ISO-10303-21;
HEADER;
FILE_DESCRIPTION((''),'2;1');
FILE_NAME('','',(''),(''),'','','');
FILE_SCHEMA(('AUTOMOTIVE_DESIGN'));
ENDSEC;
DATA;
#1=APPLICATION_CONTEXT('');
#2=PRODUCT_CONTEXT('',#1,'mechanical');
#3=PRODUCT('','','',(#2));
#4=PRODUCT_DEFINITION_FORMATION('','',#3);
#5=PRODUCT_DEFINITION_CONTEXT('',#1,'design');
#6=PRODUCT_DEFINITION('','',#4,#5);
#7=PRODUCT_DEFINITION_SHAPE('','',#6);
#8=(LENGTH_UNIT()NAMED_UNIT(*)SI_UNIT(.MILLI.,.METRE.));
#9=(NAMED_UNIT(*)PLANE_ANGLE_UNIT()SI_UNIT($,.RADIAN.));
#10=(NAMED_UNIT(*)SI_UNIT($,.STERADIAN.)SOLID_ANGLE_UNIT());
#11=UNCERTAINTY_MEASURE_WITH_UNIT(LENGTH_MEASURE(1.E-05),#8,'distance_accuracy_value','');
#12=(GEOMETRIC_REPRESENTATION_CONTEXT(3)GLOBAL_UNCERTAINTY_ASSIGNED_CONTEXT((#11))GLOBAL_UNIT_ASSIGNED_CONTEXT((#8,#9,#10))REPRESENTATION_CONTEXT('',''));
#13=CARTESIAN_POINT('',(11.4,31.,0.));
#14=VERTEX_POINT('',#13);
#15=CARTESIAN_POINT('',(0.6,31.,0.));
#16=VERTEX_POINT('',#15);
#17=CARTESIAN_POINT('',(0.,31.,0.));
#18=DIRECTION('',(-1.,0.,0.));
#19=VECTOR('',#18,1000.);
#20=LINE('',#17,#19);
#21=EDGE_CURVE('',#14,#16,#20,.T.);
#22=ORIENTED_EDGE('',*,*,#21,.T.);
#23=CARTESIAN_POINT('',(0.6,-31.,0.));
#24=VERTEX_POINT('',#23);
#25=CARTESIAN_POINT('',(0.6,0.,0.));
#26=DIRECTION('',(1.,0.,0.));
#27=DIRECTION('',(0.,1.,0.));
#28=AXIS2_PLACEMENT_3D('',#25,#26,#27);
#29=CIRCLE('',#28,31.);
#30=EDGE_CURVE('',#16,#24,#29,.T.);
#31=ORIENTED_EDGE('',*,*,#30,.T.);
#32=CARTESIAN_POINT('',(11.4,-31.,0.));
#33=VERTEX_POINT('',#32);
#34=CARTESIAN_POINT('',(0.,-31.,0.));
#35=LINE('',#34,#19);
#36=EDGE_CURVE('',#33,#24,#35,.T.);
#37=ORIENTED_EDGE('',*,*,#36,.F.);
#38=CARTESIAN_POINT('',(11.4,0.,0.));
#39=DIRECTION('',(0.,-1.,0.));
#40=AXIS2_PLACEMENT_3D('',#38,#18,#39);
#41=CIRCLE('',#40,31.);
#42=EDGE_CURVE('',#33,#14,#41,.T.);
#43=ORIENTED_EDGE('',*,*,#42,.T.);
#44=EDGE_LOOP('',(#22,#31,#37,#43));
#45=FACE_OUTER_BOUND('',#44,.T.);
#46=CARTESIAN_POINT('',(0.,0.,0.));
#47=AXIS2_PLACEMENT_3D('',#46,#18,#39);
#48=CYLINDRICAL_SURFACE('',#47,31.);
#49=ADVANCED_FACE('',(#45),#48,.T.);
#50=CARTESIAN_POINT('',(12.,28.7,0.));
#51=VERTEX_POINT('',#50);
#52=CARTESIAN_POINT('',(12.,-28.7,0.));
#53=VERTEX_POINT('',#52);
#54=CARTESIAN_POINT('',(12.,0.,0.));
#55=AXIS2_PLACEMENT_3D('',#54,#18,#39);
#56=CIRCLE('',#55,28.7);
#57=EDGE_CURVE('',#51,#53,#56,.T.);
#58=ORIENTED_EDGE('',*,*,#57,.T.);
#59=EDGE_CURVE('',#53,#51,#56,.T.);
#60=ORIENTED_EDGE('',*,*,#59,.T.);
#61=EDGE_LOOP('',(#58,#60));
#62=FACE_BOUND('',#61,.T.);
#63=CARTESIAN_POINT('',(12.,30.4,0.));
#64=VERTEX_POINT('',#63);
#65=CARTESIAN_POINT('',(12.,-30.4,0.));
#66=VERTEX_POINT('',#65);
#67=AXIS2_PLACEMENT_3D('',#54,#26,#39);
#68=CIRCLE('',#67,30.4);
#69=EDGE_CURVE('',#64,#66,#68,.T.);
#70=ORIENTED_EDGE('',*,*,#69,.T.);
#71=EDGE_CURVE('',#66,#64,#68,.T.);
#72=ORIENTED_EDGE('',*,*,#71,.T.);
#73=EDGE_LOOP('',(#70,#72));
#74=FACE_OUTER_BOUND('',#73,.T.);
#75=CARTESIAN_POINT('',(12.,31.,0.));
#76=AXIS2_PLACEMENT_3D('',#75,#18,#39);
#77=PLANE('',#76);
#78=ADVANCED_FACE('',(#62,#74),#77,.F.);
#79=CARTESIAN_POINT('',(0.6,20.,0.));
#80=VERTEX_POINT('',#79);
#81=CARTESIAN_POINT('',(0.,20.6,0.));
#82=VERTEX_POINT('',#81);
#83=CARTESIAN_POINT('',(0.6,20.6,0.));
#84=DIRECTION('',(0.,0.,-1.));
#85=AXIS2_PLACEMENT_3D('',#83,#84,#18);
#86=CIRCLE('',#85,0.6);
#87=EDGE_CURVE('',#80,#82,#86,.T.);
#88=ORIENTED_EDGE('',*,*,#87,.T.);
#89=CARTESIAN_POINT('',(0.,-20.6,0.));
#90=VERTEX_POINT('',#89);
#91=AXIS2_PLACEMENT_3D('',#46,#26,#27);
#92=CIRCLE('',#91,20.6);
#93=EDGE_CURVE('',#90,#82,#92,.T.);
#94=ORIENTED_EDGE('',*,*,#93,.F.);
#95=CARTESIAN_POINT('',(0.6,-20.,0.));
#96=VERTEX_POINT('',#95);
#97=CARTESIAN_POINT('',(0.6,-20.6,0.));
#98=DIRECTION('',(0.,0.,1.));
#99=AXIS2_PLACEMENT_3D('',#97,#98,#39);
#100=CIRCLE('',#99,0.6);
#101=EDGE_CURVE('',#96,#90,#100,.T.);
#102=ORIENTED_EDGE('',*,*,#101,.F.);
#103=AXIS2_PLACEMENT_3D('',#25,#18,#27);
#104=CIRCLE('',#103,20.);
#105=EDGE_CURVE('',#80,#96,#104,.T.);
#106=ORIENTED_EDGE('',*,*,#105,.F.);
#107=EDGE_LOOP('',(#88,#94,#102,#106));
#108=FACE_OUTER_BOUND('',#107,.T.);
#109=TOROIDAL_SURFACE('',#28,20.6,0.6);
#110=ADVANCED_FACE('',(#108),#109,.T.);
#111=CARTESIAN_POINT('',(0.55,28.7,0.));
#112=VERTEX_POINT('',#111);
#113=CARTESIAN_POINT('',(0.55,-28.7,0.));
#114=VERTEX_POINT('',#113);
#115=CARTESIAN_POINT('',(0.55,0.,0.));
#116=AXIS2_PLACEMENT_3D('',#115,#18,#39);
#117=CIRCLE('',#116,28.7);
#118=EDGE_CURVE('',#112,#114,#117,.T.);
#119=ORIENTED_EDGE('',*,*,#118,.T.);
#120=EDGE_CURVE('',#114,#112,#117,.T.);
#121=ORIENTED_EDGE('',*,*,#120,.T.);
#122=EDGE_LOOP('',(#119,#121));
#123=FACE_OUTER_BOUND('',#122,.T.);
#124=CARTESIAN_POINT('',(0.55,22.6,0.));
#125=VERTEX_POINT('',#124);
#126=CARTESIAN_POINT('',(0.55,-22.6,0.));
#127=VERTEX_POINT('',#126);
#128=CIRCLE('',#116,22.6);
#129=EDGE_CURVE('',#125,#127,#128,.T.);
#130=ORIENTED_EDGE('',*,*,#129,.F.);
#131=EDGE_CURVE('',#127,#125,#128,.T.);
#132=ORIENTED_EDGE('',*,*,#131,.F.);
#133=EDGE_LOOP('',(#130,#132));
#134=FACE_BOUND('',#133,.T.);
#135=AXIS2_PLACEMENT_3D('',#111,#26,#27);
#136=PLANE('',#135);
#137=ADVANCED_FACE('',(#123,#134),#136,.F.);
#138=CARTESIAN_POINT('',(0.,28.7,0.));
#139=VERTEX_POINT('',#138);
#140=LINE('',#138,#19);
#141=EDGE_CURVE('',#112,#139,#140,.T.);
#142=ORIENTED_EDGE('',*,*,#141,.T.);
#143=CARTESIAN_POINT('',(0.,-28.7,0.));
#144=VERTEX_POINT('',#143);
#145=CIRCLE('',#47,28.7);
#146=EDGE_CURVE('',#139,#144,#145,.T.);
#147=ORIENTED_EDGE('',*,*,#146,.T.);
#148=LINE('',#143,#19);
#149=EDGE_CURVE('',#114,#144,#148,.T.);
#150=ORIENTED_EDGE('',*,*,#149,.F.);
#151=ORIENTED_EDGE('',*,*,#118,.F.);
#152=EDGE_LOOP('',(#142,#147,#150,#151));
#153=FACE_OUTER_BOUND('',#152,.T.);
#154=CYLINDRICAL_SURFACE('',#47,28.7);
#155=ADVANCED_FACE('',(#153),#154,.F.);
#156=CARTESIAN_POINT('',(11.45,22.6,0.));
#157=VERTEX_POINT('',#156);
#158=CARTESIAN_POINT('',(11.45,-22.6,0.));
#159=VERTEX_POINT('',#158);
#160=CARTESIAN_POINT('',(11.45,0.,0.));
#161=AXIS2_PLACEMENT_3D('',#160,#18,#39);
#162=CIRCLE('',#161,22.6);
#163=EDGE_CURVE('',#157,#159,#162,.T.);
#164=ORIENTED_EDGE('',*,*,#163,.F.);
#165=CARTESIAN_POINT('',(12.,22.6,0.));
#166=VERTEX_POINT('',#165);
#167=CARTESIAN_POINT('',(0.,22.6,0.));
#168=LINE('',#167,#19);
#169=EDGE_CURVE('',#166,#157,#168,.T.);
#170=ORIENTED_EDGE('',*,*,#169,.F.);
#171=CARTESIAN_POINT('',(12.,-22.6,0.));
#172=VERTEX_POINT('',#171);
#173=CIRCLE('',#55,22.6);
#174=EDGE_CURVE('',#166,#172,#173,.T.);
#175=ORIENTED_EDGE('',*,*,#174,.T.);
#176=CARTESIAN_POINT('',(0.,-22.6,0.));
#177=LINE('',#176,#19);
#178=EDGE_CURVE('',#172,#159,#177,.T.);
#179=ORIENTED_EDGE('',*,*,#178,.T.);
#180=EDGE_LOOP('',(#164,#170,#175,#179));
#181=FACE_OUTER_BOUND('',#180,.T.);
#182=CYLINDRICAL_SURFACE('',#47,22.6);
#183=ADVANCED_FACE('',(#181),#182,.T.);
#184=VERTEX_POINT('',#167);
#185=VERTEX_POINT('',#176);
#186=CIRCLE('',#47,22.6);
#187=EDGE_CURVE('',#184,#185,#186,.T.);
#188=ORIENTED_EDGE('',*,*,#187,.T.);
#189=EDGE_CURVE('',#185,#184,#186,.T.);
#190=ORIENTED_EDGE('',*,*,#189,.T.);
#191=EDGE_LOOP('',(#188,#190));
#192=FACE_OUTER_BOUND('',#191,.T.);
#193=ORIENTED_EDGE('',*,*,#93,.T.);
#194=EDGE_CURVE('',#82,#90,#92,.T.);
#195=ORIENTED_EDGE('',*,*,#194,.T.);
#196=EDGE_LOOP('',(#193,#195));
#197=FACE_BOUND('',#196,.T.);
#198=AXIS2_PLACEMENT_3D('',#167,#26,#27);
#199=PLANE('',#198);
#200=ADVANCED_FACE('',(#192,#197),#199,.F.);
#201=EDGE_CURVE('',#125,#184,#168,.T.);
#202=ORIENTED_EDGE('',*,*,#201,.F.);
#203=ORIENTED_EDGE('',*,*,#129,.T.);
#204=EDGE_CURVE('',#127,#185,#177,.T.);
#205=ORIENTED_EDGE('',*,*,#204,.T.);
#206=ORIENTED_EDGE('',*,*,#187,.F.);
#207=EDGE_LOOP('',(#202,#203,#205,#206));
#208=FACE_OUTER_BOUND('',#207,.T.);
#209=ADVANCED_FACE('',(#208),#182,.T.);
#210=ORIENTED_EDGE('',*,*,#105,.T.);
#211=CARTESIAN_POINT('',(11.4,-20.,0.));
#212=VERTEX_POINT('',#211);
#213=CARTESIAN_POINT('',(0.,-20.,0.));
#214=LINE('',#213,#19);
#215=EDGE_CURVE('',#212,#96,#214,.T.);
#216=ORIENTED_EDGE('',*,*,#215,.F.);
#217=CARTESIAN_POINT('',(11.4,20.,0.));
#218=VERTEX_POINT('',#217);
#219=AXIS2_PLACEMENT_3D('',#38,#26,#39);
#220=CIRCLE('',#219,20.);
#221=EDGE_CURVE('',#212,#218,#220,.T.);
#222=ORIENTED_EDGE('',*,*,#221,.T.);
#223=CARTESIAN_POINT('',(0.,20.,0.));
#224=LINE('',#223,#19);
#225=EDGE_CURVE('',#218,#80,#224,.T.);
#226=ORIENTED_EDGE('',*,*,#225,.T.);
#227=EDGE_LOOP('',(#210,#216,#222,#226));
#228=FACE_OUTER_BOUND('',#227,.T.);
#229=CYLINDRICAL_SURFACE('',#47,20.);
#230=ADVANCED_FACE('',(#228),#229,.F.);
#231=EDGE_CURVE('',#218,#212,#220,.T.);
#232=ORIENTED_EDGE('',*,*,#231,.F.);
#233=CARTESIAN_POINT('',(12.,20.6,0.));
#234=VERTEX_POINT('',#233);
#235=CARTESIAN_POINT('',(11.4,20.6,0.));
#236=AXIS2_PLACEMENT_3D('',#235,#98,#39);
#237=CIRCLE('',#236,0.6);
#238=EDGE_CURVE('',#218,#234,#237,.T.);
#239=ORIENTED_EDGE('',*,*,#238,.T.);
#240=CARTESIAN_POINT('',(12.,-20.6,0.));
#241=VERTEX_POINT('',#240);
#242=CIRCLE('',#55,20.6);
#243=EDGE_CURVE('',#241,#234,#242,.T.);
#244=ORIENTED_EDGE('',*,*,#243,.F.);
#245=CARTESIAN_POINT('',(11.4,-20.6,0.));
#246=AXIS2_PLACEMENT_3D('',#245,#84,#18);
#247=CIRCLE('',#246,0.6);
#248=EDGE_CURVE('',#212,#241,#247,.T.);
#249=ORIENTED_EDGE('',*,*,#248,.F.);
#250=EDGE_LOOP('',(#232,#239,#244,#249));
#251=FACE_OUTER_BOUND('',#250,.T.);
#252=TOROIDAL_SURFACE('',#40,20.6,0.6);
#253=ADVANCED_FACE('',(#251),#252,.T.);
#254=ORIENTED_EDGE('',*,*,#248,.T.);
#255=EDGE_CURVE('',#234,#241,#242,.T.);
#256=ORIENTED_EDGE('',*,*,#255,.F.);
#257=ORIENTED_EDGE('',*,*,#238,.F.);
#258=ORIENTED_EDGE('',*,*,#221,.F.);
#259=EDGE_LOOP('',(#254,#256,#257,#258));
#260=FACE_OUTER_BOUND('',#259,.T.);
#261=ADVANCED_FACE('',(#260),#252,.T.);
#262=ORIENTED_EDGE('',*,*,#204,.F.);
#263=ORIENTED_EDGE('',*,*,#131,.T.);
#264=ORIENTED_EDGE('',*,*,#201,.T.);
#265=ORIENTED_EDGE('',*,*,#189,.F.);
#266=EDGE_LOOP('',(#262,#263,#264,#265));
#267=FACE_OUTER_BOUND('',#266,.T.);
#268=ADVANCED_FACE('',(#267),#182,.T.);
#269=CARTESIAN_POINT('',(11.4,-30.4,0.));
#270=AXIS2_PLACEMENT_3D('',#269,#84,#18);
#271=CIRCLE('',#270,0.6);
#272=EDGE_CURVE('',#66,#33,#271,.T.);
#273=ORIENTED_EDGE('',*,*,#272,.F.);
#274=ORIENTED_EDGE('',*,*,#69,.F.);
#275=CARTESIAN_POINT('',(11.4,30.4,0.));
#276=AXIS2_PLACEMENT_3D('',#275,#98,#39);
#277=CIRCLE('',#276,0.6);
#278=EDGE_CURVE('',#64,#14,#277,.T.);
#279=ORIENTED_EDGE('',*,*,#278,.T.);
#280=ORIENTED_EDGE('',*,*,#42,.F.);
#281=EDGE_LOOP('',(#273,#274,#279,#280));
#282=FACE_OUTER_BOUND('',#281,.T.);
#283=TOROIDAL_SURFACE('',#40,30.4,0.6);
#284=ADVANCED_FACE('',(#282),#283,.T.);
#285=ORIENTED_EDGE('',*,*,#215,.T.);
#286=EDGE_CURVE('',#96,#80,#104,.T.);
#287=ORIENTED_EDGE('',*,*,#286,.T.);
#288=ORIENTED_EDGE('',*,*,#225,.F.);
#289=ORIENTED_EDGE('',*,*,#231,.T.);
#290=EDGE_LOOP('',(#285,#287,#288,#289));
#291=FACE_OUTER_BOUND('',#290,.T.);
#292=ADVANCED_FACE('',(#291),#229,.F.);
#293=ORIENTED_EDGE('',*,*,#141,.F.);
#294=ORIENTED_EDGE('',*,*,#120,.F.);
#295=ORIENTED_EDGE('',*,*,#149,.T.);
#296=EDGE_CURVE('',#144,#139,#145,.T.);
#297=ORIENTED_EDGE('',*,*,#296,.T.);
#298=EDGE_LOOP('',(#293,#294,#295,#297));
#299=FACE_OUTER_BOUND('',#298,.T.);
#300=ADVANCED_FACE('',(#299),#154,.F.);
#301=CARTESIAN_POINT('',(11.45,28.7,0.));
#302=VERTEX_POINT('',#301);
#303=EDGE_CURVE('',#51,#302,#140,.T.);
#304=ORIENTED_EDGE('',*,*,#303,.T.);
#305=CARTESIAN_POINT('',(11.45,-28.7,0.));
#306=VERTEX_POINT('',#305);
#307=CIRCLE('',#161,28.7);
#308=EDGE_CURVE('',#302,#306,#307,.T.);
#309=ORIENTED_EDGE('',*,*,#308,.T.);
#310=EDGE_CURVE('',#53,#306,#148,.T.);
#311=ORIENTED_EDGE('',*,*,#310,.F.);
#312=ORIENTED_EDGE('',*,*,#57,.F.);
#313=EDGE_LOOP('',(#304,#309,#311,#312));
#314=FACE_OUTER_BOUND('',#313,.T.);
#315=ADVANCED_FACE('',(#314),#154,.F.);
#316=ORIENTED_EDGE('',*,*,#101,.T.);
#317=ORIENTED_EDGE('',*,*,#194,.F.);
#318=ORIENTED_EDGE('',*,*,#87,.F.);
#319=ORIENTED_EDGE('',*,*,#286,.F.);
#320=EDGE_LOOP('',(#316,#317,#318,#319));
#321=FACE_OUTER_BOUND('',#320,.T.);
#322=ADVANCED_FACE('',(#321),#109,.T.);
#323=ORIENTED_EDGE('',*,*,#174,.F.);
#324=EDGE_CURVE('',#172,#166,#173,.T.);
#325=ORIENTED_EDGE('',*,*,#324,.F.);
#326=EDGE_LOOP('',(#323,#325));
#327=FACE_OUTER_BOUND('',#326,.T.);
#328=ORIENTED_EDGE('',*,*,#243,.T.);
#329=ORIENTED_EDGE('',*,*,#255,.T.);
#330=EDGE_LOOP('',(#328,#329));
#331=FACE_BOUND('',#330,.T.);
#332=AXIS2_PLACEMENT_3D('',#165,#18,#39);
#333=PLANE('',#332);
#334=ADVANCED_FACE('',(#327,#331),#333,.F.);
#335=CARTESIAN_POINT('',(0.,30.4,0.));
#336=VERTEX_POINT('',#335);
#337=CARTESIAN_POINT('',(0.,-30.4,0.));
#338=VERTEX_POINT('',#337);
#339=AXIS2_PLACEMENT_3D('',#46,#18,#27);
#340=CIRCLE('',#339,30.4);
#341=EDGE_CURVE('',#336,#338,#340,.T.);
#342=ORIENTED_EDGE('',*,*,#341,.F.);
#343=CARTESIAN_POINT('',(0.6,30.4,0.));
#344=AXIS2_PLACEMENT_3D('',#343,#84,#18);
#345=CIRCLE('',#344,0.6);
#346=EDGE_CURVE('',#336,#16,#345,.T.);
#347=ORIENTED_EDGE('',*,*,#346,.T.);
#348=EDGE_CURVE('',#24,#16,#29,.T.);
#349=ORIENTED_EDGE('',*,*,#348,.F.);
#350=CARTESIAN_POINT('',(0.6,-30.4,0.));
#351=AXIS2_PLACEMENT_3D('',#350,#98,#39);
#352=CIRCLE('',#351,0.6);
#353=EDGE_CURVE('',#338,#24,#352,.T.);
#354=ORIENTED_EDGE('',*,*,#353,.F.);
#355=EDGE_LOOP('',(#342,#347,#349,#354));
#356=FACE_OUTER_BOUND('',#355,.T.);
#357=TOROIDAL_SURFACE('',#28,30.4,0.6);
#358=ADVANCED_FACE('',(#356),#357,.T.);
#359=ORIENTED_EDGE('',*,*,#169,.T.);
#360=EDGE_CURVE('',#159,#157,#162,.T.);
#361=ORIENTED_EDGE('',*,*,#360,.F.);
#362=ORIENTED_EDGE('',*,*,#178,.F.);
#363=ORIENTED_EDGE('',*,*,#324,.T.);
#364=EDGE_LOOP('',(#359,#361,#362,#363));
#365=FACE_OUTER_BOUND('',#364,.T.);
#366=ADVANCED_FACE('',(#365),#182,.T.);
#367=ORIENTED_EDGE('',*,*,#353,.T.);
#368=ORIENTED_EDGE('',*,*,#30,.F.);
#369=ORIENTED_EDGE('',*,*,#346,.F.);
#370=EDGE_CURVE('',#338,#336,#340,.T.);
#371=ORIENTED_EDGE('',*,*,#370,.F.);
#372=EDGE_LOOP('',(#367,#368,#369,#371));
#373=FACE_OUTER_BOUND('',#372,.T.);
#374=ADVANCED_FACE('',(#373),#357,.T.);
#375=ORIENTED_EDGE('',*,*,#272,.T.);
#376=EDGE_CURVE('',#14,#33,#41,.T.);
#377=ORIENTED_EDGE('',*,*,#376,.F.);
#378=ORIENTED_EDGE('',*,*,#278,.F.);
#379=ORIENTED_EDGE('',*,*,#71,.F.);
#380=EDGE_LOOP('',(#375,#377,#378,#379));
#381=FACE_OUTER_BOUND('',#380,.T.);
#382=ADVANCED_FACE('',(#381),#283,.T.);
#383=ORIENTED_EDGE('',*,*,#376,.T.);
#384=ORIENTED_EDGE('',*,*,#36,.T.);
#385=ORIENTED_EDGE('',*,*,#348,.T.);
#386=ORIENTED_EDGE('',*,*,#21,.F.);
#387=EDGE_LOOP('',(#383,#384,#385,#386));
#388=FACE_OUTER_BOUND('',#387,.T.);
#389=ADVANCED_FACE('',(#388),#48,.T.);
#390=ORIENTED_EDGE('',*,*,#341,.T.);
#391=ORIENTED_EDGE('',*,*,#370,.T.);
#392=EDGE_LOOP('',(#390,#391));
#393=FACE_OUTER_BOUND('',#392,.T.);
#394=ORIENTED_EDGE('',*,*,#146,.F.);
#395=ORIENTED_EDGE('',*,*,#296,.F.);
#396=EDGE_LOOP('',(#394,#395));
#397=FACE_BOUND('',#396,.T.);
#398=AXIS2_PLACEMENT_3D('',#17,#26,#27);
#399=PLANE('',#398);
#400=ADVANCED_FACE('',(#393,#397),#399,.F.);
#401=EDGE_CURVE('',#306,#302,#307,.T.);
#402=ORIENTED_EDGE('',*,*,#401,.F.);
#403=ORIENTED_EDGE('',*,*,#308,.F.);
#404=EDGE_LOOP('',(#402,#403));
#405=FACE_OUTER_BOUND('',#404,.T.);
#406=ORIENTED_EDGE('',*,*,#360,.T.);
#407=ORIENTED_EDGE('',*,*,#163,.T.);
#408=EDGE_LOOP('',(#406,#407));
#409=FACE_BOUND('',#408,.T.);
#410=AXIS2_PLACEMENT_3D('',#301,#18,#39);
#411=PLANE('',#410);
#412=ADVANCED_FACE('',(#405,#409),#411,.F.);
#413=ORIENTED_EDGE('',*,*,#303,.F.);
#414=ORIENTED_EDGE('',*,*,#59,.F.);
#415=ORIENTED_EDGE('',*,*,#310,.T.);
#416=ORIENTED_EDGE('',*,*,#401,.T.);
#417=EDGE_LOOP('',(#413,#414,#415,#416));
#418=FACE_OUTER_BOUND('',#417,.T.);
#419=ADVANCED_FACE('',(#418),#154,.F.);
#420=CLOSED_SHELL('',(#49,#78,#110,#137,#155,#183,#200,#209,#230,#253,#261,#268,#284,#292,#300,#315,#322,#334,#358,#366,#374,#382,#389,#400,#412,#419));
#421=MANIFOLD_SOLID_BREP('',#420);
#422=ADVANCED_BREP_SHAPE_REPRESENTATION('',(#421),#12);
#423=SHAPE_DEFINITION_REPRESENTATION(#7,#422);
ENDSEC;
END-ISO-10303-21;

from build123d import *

# Parameters (mm, degrees)
FILLET1_R = 0.6
FILLET2_R = 0.6


with BuildPart() as part:
    # Sketch1 → Revolve1 (revolve)
    with BuildSketch(Plane.XY, mode=Mode.PRIVATE) as revolve1_sk:
        Polygon((0, 20), (12, 20), (12, 22.6), (11.45, 22.6), (11.45, 28.7), (12, 28.7), (12, 31), (0, 31), (0, 28.7), (0.55, 28.7), (0.55, 22.6), (0, 22.6), align=None)
    revolve(revolve1_sk.sketch.rotate(Axis((0, 0, 0), (1, 0, 0)), 180), axis=Axis((0, 0, 0), (1, 0, 0)))

    # Fillet1
    fillet1_edges = [part.edges().sort_by_distance(p)[0] for p in [
        (0, 31, 0),
        (12, 31, 0),
    ]]
    fillet(fillet1_edges, radius=FILLET1_R)

    # Fillet2
    fillet2_edges = [part.edges().sort_by_distance(p)[0] for p in [
        (12, 20, 0),
        (0, 20, 0),
    ]]
    fillet(fillet2_edges, radius=FILLET2_R)


solid = part.part
